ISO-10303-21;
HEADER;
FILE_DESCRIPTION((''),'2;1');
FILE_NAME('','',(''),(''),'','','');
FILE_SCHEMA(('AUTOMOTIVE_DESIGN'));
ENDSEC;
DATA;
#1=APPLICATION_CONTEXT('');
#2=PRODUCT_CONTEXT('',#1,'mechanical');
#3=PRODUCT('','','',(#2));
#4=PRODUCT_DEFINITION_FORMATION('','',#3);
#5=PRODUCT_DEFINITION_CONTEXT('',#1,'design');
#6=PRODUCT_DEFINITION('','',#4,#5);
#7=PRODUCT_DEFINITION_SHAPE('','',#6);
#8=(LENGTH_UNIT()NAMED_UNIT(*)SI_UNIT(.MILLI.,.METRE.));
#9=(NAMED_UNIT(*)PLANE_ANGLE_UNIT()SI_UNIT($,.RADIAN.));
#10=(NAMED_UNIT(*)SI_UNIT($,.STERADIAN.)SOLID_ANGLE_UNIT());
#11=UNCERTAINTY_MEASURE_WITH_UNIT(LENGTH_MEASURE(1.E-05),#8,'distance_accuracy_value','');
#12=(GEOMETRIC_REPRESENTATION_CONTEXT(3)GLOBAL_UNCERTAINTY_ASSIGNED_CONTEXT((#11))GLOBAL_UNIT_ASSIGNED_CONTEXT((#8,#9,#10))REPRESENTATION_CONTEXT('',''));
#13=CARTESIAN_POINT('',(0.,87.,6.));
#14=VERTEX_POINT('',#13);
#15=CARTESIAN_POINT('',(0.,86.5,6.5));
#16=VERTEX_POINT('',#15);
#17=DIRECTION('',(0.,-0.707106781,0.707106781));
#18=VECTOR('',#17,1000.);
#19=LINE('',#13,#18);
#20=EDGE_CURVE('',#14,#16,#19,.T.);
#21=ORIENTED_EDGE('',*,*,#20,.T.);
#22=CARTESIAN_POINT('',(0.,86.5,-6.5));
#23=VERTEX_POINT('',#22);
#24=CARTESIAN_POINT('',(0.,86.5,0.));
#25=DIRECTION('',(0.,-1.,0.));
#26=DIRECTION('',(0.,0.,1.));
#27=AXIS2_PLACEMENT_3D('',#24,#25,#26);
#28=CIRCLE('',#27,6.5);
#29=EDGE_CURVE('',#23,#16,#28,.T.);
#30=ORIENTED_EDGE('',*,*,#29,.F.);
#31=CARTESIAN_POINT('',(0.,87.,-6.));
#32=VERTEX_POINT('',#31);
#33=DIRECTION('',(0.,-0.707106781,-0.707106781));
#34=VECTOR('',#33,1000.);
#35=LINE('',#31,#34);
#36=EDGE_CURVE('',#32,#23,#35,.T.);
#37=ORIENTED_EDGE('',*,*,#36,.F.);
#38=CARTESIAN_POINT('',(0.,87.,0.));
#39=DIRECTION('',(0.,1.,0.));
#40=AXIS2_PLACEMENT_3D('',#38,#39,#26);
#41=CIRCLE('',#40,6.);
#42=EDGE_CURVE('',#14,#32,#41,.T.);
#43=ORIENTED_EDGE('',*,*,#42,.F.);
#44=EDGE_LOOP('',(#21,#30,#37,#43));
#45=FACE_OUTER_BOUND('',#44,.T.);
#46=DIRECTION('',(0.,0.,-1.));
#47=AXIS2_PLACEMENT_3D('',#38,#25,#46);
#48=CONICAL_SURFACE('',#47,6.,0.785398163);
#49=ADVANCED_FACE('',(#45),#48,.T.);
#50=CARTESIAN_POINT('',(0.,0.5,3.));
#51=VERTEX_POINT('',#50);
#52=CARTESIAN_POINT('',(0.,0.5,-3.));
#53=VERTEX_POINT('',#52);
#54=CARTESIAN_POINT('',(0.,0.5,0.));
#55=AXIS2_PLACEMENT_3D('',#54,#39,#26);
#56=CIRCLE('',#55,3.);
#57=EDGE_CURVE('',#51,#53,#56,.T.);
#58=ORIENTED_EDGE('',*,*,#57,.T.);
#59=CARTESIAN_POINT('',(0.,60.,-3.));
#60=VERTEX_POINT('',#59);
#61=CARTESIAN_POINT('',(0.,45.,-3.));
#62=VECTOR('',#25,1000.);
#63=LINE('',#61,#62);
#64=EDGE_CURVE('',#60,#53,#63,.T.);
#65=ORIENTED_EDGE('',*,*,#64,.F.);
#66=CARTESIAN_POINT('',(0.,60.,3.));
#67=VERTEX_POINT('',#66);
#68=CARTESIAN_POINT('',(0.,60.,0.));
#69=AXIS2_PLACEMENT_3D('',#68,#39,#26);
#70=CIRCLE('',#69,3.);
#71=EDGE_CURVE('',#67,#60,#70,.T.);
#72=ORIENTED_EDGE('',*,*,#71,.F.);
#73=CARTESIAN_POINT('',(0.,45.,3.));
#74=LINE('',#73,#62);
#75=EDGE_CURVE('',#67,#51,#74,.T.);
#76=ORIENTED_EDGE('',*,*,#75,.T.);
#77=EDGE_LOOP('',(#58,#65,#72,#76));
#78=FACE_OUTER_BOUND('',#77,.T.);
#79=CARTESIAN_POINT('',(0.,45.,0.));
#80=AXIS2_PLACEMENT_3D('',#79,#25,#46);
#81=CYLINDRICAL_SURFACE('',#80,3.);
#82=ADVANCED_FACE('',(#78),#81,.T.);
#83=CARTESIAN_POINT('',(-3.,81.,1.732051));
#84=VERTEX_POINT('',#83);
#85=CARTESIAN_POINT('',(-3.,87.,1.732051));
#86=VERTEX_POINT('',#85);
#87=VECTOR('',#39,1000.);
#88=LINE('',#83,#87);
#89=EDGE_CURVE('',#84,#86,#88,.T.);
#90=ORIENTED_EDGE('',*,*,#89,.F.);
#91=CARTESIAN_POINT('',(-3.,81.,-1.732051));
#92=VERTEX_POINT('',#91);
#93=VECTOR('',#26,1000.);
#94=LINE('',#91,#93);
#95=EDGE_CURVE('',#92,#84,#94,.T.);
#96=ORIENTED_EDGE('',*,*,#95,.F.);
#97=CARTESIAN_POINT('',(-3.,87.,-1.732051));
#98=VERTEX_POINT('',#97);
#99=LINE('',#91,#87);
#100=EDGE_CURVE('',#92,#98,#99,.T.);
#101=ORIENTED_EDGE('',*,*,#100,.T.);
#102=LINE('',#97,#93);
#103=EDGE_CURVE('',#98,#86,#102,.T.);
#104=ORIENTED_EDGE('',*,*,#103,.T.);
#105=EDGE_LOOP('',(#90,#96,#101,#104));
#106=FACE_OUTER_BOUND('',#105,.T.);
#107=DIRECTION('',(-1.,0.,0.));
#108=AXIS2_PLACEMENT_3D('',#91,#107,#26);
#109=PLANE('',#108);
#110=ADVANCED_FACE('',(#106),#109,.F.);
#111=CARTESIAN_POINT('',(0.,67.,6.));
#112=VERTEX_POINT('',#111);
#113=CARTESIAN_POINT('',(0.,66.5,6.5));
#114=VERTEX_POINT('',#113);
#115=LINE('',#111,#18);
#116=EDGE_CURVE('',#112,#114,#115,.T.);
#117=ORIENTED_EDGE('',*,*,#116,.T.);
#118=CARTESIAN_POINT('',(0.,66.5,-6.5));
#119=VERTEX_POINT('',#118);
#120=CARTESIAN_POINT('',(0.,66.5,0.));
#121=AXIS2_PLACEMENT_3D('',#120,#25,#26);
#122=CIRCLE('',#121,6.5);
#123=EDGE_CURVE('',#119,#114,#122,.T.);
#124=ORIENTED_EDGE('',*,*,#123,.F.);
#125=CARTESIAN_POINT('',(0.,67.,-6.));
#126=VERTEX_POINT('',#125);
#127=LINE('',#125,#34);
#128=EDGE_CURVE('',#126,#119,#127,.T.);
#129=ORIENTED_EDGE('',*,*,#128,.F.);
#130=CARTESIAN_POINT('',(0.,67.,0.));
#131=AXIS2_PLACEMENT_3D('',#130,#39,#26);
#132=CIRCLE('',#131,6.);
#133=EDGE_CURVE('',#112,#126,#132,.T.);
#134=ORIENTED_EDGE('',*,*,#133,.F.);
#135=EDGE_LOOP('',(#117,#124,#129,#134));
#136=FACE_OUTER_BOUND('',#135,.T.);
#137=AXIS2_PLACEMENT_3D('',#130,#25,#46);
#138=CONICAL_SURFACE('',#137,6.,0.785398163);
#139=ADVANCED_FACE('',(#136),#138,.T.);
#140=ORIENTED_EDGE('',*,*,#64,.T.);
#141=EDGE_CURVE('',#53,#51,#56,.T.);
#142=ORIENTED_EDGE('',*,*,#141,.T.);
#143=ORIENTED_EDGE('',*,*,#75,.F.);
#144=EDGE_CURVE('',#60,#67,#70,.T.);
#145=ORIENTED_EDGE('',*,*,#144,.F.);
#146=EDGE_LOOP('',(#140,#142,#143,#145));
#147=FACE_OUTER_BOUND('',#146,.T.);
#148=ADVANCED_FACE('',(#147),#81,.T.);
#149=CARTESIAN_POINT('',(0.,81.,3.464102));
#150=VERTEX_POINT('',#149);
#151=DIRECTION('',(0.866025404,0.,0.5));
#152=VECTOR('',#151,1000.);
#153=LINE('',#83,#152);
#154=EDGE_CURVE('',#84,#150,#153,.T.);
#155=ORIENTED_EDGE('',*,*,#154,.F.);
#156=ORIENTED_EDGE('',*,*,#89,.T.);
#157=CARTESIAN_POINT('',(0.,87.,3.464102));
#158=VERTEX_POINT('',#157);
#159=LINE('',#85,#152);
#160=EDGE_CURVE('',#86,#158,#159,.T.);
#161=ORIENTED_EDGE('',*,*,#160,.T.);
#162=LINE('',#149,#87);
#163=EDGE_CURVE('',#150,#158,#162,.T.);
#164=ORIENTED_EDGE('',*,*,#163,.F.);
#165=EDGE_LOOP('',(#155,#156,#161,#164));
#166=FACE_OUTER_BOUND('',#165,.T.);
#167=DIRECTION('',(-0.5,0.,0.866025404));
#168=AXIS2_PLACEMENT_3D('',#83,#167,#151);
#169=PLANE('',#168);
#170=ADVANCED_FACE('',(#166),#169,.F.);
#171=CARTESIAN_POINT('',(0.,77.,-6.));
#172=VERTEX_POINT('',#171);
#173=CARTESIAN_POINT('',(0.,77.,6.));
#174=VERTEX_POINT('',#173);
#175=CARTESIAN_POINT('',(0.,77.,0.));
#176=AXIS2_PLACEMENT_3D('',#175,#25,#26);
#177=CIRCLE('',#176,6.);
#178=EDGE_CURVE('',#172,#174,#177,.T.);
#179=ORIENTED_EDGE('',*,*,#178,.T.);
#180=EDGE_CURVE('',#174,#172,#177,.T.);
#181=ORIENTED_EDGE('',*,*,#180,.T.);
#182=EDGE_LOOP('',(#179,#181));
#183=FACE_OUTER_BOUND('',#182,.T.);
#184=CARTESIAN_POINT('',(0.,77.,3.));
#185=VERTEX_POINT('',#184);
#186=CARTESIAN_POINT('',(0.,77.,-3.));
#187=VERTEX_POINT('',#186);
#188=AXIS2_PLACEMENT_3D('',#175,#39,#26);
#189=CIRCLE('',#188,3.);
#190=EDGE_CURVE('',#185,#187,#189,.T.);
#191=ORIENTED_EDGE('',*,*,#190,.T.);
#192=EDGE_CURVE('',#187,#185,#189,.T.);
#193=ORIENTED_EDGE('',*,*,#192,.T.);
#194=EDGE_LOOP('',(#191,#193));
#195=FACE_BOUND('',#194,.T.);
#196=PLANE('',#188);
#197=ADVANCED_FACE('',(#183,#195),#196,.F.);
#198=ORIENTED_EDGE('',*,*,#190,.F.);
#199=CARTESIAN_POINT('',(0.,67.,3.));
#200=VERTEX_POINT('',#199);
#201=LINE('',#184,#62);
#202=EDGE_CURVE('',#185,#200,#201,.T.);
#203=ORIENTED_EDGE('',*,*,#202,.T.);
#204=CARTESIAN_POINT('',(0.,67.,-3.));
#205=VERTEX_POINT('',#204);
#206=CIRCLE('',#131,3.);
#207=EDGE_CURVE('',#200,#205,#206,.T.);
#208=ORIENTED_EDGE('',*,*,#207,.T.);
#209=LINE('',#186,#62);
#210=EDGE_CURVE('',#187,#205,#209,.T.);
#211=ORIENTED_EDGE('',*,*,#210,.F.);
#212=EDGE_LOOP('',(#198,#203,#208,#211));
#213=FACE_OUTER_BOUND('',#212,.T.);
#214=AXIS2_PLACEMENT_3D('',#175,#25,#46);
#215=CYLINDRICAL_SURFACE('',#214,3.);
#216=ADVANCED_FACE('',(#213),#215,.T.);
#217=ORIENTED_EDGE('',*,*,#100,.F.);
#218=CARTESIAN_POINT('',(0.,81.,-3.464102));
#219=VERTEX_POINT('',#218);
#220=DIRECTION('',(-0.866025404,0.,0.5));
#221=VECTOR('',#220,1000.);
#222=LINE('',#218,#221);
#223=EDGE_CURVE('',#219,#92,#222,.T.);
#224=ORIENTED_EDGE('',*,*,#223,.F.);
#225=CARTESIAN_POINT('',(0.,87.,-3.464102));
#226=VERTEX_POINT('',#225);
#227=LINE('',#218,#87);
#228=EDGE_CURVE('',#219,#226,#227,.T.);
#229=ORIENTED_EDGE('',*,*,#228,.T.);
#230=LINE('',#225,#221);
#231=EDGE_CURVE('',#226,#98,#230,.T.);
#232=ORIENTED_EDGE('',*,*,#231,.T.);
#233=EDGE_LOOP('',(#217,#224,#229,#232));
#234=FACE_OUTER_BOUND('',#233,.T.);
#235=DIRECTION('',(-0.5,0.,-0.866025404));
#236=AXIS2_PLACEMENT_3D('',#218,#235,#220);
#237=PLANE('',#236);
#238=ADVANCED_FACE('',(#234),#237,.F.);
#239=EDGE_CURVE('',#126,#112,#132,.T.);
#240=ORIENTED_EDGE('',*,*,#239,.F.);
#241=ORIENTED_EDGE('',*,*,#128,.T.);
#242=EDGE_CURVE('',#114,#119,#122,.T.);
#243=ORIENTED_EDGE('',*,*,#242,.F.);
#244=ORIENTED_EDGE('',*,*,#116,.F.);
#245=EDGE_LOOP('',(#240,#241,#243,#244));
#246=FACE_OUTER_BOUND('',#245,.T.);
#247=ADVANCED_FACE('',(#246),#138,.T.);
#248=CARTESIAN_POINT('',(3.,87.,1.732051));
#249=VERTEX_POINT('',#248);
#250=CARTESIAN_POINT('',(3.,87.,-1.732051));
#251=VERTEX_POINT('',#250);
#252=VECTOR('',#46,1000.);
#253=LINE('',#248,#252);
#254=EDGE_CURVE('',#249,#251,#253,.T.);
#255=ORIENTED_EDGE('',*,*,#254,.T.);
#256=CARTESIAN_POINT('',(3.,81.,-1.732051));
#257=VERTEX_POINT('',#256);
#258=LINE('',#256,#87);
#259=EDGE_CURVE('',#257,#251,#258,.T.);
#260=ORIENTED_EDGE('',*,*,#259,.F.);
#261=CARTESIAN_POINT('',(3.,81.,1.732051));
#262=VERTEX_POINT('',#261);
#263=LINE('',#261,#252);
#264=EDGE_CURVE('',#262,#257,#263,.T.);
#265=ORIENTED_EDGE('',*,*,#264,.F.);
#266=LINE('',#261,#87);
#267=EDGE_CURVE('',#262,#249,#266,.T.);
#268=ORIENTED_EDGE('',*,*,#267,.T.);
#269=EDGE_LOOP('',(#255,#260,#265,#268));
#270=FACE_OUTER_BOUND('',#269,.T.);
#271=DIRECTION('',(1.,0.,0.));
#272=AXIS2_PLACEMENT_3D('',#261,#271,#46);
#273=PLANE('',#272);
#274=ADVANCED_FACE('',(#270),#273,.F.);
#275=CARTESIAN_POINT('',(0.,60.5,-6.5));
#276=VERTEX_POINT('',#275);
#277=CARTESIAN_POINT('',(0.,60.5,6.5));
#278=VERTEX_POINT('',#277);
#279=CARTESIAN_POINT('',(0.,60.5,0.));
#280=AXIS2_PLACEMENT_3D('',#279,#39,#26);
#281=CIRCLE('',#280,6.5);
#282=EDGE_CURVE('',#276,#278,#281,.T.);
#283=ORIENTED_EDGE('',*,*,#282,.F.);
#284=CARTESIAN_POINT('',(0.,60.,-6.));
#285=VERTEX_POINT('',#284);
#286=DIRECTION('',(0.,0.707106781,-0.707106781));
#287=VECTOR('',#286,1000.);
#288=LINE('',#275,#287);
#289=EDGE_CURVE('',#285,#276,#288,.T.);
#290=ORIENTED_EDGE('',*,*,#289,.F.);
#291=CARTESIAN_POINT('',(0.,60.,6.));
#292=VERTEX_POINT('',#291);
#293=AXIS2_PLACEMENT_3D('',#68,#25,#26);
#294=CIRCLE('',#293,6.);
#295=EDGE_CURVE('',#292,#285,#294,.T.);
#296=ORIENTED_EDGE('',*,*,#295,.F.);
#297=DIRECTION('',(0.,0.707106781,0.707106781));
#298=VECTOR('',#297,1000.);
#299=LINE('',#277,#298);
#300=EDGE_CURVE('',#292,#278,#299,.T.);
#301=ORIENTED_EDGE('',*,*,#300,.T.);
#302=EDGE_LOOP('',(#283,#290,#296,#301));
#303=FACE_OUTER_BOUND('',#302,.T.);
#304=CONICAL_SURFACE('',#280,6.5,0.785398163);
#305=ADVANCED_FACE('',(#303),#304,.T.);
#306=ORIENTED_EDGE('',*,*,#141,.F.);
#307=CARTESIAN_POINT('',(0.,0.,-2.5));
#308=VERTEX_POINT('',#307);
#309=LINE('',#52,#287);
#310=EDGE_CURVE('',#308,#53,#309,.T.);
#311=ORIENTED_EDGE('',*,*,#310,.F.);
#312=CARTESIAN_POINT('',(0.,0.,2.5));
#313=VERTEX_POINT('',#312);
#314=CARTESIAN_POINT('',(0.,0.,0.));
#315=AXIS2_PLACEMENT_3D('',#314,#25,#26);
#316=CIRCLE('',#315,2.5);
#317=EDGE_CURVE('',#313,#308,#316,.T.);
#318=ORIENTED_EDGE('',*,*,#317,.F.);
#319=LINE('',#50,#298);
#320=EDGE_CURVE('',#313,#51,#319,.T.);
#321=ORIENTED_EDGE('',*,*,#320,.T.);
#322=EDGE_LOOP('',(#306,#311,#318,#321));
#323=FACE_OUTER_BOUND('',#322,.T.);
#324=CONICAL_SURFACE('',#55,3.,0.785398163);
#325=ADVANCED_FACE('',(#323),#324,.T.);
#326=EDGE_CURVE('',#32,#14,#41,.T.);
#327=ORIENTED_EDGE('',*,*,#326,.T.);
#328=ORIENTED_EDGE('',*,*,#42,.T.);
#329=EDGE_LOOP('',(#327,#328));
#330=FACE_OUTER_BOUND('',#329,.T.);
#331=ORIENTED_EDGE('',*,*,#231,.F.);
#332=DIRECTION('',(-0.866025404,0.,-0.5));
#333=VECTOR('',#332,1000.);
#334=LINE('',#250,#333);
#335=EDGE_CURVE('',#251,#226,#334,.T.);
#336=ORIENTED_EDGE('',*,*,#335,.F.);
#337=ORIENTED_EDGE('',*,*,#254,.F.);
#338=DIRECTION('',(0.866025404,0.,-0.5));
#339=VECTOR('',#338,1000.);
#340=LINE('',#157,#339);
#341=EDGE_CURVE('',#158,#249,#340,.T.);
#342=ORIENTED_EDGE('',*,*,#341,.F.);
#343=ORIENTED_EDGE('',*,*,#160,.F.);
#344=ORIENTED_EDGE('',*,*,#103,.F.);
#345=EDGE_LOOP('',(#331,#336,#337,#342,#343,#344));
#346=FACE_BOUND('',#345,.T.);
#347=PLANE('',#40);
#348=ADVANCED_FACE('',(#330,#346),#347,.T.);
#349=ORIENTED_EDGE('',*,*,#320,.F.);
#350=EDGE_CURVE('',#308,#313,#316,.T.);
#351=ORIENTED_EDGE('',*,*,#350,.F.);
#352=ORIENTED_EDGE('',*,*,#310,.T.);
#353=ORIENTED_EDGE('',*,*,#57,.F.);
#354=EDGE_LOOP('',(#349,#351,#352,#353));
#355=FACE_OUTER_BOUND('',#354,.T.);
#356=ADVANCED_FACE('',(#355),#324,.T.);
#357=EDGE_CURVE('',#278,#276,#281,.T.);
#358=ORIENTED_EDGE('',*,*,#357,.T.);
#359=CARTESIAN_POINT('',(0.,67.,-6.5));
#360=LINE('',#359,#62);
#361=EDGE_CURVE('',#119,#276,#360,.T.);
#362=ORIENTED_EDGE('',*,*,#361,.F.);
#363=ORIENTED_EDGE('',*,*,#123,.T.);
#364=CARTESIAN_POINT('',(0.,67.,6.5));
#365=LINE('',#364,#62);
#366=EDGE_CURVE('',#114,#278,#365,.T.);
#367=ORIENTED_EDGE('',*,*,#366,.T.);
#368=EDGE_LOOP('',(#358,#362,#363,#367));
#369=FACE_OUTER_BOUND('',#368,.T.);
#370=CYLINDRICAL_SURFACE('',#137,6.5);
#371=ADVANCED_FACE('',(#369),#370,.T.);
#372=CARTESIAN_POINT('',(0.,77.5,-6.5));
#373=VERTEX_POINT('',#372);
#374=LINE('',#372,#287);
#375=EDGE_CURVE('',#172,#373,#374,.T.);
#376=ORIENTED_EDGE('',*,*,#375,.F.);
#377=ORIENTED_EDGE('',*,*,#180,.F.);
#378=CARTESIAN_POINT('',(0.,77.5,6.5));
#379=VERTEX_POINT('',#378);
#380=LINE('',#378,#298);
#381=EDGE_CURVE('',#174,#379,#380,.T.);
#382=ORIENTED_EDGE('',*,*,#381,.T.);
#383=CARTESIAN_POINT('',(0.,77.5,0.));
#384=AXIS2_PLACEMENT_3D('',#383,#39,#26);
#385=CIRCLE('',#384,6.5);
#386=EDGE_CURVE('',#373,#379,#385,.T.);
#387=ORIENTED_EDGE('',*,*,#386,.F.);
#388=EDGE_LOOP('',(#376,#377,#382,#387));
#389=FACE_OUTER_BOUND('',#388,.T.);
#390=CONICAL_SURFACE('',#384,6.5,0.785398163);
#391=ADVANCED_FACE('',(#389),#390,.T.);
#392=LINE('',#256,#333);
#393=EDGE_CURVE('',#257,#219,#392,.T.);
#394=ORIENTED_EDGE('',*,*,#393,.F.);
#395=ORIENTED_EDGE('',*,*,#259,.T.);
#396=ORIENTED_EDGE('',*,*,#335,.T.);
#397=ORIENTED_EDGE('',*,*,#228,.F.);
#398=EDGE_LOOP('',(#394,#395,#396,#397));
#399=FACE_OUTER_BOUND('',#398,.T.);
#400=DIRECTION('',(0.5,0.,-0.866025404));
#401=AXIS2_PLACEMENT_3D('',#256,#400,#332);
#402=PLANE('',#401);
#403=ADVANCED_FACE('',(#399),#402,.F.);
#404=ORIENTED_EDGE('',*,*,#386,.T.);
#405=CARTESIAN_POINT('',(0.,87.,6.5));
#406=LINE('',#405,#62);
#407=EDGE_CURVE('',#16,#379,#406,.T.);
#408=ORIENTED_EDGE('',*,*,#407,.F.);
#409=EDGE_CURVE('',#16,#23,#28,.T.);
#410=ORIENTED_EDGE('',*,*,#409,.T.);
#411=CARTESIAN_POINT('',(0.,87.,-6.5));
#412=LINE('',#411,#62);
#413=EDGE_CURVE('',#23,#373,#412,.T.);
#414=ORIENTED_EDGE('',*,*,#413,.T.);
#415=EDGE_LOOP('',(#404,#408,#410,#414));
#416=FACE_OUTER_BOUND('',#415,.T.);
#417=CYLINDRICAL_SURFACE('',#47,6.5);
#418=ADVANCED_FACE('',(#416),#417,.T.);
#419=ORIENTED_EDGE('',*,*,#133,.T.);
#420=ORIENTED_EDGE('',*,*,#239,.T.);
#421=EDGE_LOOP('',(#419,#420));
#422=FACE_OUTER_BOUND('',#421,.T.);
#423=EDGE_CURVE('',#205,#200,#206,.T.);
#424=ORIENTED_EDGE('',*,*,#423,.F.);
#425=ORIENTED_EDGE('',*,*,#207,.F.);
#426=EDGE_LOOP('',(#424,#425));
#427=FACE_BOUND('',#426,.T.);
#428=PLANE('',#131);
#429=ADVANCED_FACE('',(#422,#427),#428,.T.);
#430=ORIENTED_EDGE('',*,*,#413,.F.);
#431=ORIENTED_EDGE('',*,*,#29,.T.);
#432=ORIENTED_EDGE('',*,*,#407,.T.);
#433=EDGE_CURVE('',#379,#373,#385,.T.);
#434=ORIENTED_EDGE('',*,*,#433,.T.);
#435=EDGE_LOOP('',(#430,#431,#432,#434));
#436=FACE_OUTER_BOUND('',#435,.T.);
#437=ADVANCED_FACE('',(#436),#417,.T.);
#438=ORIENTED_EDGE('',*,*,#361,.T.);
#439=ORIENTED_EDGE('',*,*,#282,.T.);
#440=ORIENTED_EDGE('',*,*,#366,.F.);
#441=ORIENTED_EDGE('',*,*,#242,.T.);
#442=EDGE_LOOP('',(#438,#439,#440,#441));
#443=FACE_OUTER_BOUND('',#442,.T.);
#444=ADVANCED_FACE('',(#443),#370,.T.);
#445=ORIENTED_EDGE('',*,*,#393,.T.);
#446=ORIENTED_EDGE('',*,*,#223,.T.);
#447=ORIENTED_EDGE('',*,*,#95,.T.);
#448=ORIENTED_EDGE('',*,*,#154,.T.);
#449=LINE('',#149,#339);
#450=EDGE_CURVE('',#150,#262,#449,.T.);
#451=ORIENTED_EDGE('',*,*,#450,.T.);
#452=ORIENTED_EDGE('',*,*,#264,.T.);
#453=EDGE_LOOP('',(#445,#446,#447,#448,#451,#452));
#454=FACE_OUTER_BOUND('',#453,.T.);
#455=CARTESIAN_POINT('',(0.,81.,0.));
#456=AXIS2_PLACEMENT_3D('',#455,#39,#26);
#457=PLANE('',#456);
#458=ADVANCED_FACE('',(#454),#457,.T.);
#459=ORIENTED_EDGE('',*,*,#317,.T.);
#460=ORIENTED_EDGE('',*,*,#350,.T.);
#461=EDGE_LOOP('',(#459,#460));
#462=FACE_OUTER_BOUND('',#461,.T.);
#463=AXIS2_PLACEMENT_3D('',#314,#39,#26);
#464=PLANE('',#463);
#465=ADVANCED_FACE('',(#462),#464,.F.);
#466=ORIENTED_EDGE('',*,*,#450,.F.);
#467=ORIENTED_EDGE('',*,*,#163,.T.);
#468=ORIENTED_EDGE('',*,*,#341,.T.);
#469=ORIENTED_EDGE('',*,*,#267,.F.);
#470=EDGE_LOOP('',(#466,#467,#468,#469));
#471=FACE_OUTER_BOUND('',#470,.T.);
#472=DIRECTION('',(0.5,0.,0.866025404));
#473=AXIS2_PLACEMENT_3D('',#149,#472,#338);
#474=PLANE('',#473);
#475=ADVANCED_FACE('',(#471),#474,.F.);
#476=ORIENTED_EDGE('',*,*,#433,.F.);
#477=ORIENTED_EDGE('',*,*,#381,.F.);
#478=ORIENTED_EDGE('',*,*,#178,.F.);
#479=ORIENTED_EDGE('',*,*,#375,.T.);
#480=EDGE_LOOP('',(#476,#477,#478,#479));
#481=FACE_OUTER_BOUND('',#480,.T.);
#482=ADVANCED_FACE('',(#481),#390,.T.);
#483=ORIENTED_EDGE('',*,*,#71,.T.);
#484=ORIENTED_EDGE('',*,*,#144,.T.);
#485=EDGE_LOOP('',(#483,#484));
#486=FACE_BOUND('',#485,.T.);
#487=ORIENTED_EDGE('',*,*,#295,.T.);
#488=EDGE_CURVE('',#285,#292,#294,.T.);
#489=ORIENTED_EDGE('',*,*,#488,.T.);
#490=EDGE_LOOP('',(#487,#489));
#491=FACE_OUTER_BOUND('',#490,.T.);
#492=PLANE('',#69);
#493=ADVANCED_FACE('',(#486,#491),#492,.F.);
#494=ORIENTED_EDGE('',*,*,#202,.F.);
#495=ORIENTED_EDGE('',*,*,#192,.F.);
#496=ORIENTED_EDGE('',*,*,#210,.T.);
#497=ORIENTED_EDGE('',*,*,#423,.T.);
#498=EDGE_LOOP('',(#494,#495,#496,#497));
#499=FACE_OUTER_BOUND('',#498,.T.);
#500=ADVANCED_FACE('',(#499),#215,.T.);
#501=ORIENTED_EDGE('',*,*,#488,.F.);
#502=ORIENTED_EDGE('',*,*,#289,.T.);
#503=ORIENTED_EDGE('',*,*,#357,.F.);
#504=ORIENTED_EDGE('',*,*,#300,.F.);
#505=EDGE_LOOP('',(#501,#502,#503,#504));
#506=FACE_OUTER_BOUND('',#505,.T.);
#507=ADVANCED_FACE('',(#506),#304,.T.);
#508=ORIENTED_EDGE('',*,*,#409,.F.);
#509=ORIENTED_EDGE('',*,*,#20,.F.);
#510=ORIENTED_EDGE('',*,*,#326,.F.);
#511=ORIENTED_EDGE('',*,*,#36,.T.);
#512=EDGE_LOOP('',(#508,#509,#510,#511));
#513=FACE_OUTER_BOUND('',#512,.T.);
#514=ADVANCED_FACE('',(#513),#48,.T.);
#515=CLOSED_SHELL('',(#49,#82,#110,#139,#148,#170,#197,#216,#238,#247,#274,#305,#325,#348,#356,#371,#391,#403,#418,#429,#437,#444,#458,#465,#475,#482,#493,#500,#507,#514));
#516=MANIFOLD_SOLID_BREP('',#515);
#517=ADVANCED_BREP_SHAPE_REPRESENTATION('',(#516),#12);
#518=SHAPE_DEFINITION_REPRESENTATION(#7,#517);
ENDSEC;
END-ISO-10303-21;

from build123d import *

# Parameters (mm, degrees)
SKETCH1_R           = 3
BOSS_EXTRUDE1_DEPTH = 45
SKETCH2_R           = 3
BOSS_EXTRUDE2_DEPTH = 15
SKETCH3_R           = 6.5
BOSS_EXTRUDE3_DEPTH = 7
SKETCH4_R           = 3
BOSS_EXTRUDE4_DEPTH = 10
SKETCH5_R           = 6.5
BOSS_EXTRUDE5_DEPTH = 10
CUT_EXTRUDE1_DEPTH  = 6
CHAMFER1_SIZE       = 0.5


with BuildPart() as part:
    # Sketch1 → Boss-Extrude1 (new body)
    with BuildSketch(Plane(origin=(0, 0, 0), x_dir=(1, 0, 0), z_dir=(0, 1, 0))):
        with Locations(Location((0, 0, 0), (0, 0, 90))):
            Circle(SKETCH1_R)
    extrude(amount=BOSS_EXTRUDE1_DEPTH)

    # Sketch2 → Boss-Extrude2 (add)
    with BuildSketch(Plane(origin=(0, 45, 0), x_dir=(1, 0, 0), z_dir=(0, 1, 0))):
        with Locations(Location((0, 0, 0), (0, 0, 90))):
            Circle(SKETCH2_R)
    extrude(amount=BOSS_EXTRUDE2_DEPTH)

    # Sketch3 → Boss-Extrude3 (add)
    with BuildSketch(Plane(origin=(0, 60, 0), x_dir=(1, 0, 0), z_dir=(0, 1, 0))):
        with Locations(Location((0, 0, 0), (0, 0, 270))):
            Circle(SKETCH3_R)
    extrude(amount=BOSS_EXTRUDE3_DEPTH)

    # Sketch4 → Boss-Extrude4 (add)
    with BuildSketch(Plane(origin=(0, 67, 0), x_dir=(1, 0, 0), z_dir=(0, 1, 0))):
        with Locations(Location((0, 0, 0), (0, 0, 90))):
            Circle(SKETCH4_R)
    extrude(amount=BOSS_EXTRUDE4_DEPTH)

    # Sketch5 → Boss-Extrude5 (add)
    with BuildSketch(Plane(origin=(0, 77, 0), x_dir=(1, 0, 0), z_dir=(0, 1, 0))):
        with Locations(Location((0, 0, 0), (0, 0, 270))):
            Circle(SKETCH5_R)
    extrude(amount=BOSS_EXTRUDE5_DEPTH)

    # Sketch6 → Cut-Extrude1 (cut)
    with BuildSketch(Plane(origin=(0, 87, 0), x_dir=(1, 0, 0), z_dir=(0, 1, 0))):
        Polygon((0, 3.464101615), (-3, 1.732050808), (-3, -1.732050808), (0, -3.464101615), (3, -1.732050808), (3, 1.732050808), align=None)
    extrude(amount=-CUT_EXTRUDE1_DEPTH, mode=Mode.SUBTRACT)

    # Chamfer1
    chamfer1_edges = [part.edges().sort_by_distance(p)[0] for p in [
        (0, 77, -6.5),
        (0, 87, -6.5),
        (0, 0, 3),
        (0, 60, -6.5),
        (0, 67, -6.5),
    ]]
    chamfer(chamfer1_edges, length=CHAMFER1_SIZE)


solid = part.part
